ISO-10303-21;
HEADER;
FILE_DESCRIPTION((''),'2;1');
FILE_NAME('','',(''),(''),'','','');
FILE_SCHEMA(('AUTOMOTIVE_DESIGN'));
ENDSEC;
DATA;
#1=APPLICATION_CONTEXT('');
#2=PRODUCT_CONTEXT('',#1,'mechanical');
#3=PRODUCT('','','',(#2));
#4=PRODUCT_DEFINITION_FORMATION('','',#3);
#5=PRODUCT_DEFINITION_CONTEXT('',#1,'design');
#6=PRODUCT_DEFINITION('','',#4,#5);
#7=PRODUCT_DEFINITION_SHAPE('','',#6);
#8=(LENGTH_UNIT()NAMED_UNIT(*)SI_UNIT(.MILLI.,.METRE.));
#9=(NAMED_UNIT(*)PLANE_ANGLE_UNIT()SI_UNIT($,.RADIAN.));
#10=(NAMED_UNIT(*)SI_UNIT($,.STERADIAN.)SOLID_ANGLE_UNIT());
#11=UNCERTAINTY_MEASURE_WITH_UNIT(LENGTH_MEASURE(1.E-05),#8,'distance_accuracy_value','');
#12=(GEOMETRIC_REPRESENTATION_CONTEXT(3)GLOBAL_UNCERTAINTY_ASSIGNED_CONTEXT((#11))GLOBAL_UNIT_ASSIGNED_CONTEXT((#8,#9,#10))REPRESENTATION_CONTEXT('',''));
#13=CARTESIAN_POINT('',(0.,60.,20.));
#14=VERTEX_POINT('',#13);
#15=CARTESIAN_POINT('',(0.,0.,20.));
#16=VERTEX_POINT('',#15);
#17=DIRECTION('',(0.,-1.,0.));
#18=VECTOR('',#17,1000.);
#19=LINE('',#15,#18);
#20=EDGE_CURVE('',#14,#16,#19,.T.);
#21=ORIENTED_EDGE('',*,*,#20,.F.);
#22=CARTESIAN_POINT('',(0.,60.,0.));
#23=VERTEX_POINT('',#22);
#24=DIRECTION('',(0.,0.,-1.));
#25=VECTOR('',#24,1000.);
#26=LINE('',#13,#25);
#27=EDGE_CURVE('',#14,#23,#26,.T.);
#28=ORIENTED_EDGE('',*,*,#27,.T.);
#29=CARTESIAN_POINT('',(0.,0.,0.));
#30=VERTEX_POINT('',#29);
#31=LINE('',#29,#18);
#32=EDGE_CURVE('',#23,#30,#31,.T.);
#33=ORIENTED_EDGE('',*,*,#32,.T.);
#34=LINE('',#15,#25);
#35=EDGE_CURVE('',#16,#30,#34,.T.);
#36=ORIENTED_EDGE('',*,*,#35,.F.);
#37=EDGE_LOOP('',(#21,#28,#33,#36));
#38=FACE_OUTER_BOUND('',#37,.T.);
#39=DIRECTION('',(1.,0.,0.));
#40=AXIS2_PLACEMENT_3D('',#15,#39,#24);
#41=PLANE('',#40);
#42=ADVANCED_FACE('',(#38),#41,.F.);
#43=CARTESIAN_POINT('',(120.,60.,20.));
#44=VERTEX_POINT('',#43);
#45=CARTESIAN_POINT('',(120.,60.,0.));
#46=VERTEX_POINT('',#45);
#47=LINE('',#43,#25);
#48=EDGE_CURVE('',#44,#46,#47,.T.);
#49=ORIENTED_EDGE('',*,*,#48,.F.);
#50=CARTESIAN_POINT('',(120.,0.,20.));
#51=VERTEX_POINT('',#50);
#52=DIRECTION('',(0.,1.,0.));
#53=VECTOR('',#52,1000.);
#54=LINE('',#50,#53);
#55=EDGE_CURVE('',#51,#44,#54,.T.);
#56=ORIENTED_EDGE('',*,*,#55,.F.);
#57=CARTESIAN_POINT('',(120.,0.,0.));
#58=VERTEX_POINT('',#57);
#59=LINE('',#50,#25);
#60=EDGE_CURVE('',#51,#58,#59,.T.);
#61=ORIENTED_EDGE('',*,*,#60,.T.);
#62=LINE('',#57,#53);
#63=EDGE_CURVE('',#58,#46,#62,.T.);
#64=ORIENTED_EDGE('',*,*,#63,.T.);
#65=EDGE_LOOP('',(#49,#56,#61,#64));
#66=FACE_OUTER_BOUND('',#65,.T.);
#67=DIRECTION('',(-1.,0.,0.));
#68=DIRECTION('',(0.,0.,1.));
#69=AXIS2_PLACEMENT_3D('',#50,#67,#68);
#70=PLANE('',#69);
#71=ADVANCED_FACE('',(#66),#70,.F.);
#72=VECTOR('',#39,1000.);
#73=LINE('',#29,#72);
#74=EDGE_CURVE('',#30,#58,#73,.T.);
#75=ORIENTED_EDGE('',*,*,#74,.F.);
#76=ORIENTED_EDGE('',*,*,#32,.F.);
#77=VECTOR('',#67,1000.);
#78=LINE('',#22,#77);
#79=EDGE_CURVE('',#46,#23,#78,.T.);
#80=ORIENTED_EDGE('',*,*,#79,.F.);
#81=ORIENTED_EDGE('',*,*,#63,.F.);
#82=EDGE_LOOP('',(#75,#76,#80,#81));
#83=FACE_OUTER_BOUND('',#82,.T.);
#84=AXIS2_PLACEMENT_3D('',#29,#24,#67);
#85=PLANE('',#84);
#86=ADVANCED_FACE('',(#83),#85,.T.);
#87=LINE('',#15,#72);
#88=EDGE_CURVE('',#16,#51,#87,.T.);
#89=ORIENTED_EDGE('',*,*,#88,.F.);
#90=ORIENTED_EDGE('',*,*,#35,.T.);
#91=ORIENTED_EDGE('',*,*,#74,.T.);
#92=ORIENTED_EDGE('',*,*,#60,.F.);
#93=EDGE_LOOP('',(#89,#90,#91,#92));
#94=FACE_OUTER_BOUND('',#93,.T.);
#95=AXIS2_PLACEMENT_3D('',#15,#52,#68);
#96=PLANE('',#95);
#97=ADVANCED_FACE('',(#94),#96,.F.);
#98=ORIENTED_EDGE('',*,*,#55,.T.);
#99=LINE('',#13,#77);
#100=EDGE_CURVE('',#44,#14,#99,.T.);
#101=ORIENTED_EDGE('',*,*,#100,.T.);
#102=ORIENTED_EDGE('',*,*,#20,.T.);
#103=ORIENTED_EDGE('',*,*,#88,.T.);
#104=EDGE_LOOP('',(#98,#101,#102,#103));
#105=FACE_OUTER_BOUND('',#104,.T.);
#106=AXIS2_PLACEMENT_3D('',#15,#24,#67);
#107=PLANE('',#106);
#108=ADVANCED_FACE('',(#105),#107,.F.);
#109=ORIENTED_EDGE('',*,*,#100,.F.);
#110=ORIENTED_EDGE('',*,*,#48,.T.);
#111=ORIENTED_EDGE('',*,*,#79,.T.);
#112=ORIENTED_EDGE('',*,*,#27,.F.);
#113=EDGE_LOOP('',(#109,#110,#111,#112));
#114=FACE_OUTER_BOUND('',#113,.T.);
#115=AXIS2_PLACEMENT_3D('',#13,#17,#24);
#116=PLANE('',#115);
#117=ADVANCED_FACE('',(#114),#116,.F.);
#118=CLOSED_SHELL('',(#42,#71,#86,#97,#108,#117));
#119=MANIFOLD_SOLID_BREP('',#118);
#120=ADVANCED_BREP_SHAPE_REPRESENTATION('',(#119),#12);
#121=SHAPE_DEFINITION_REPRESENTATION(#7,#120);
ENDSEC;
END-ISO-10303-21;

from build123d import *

# Parameters (mm, degrees)
SKETCH1_W           = 120
SKETCH1_H           = 60
BOSS_EXTRUDE1_DEPTH = 20


with BuildPart() as part:
    # Sketch1 → Boss-Extrude1 (new body)
    with BuildSketch(Plane.XY):
        with Locations((60, 30)):
            Rectangle(SKETCH1_W, SKETCH1_H)
    extrude(amount=BOSS_EXTRUDE1_DEPTH)


solid = part.part
